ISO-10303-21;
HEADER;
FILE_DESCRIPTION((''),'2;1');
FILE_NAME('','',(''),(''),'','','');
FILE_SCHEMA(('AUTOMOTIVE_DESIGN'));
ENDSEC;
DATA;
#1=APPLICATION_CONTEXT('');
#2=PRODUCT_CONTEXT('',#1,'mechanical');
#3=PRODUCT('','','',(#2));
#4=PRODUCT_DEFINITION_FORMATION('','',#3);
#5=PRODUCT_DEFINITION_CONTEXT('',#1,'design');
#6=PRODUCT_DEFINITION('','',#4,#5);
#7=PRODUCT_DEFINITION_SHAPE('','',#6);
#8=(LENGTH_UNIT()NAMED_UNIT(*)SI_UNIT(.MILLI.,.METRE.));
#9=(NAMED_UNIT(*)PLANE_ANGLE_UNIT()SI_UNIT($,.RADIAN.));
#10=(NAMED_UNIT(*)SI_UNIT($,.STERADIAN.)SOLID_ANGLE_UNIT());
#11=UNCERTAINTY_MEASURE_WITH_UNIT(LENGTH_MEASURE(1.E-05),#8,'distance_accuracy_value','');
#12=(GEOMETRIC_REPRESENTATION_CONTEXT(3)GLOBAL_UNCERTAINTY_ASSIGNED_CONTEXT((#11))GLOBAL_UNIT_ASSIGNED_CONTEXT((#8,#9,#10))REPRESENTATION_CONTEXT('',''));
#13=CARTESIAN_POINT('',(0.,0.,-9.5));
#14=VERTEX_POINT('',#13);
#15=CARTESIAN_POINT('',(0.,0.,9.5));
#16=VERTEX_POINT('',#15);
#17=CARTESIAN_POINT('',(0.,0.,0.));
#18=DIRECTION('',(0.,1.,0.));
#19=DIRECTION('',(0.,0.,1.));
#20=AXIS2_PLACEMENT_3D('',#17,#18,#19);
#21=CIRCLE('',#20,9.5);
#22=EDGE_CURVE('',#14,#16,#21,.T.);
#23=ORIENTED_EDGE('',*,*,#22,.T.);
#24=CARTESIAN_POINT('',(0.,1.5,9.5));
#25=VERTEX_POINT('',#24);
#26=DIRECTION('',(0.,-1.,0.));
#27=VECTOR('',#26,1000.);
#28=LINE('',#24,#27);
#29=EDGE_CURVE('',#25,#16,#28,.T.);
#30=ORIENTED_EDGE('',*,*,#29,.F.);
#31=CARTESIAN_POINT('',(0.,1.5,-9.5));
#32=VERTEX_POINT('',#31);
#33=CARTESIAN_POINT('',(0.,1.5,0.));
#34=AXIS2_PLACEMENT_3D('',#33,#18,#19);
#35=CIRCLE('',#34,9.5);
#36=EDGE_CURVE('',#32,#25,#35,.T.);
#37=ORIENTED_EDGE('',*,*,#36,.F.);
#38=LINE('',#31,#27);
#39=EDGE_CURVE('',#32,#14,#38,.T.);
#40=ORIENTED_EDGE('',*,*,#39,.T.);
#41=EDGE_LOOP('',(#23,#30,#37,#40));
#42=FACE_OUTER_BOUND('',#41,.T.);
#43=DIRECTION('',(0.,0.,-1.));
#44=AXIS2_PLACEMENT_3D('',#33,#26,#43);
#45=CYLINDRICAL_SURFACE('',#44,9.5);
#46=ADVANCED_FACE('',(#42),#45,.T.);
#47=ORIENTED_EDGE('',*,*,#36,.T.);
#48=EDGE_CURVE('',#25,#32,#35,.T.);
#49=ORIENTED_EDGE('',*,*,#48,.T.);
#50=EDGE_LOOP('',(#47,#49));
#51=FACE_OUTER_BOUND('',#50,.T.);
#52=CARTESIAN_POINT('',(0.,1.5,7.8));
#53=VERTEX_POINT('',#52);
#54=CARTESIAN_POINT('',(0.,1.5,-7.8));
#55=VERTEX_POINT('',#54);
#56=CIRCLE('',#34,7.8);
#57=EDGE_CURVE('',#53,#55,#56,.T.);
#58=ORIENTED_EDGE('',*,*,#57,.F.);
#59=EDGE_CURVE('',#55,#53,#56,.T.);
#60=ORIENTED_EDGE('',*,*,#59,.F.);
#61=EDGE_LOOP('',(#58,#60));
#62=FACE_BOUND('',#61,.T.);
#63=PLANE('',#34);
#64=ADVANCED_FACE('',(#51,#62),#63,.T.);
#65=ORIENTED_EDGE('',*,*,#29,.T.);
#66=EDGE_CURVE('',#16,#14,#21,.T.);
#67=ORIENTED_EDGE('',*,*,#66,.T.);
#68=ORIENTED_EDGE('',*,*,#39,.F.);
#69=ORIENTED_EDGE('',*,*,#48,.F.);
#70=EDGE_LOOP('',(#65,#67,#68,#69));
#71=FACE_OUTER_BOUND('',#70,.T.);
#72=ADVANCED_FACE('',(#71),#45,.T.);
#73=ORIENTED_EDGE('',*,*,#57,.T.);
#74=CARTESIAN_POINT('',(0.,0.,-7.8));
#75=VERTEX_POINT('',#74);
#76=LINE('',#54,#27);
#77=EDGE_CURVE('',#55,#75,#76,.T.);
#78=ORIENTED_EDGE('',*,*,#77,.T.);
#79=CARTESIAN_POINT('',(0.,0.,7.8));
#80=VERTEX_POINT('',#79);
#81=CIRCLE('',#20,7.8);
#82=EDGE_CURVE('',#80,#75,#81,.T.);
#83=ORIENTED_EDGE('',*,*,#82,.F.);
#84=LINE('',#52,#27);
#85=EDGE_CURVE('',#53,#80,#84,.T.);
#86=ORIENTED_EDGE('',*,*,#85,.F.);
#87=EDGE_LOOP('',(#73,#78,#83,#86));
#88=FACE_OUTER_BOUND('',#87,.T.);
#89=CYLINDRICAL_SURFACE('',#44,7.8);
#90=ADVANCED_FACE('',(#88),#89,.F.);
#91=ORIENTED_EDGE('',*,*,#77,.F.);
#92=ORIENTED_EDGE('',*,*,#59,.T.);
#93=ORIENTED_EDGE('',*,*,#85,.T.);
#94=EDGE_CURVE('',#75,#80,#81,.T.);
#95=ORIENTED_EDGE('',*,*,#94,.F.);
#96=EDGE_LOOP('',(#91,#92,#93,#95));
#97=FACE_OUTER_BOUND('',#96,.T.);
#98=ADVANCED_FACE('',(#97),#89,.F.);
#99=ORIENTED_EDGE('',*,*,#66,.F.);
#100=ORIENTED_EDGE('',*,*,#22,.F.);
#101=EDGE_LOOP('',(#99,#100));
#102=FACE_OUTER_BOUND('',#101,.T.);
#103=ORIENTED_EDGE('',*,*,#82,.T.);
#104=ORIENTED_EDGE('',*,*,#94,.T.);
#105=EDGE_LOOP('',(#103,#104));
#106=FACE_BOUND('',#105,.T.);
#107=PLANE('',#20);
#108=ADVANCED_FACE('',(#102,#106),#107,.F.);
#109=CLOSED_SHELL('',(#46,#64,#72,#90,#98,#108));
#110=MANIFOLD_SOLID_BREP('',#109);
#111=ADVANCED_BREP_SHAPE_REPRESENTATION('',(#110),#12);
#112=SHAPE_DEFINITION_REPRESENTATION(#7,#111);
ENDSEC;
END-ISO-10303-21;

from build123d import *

# Parameters (mm, degrees)
SKETCH_1_R      = 9.5
SKETCH_1_R_2    = 7.8
EXTRUDE_1_DEPTH = 1.5


with BuildPart() as part:
    # 草图1 → 拉伸1 (new body)
    with BuildSketch(Plane(origin=(0, 0, 0), x_dir=(1, 0, 0), z_dir=(0, 1, 0))):
        with Locations(Location((0, 0, 0), (0, 0, 270))):
            Circle(SKETCH_1_R)
        with Locations(Location((0, 0, 0), (0, 0, 270))):
            Circle(SKETCH_1_R_2, mode=Mode.SUBTRACT)
    extrude(amount=EXTRUDE_1_DEPTH)


solid = part.part
